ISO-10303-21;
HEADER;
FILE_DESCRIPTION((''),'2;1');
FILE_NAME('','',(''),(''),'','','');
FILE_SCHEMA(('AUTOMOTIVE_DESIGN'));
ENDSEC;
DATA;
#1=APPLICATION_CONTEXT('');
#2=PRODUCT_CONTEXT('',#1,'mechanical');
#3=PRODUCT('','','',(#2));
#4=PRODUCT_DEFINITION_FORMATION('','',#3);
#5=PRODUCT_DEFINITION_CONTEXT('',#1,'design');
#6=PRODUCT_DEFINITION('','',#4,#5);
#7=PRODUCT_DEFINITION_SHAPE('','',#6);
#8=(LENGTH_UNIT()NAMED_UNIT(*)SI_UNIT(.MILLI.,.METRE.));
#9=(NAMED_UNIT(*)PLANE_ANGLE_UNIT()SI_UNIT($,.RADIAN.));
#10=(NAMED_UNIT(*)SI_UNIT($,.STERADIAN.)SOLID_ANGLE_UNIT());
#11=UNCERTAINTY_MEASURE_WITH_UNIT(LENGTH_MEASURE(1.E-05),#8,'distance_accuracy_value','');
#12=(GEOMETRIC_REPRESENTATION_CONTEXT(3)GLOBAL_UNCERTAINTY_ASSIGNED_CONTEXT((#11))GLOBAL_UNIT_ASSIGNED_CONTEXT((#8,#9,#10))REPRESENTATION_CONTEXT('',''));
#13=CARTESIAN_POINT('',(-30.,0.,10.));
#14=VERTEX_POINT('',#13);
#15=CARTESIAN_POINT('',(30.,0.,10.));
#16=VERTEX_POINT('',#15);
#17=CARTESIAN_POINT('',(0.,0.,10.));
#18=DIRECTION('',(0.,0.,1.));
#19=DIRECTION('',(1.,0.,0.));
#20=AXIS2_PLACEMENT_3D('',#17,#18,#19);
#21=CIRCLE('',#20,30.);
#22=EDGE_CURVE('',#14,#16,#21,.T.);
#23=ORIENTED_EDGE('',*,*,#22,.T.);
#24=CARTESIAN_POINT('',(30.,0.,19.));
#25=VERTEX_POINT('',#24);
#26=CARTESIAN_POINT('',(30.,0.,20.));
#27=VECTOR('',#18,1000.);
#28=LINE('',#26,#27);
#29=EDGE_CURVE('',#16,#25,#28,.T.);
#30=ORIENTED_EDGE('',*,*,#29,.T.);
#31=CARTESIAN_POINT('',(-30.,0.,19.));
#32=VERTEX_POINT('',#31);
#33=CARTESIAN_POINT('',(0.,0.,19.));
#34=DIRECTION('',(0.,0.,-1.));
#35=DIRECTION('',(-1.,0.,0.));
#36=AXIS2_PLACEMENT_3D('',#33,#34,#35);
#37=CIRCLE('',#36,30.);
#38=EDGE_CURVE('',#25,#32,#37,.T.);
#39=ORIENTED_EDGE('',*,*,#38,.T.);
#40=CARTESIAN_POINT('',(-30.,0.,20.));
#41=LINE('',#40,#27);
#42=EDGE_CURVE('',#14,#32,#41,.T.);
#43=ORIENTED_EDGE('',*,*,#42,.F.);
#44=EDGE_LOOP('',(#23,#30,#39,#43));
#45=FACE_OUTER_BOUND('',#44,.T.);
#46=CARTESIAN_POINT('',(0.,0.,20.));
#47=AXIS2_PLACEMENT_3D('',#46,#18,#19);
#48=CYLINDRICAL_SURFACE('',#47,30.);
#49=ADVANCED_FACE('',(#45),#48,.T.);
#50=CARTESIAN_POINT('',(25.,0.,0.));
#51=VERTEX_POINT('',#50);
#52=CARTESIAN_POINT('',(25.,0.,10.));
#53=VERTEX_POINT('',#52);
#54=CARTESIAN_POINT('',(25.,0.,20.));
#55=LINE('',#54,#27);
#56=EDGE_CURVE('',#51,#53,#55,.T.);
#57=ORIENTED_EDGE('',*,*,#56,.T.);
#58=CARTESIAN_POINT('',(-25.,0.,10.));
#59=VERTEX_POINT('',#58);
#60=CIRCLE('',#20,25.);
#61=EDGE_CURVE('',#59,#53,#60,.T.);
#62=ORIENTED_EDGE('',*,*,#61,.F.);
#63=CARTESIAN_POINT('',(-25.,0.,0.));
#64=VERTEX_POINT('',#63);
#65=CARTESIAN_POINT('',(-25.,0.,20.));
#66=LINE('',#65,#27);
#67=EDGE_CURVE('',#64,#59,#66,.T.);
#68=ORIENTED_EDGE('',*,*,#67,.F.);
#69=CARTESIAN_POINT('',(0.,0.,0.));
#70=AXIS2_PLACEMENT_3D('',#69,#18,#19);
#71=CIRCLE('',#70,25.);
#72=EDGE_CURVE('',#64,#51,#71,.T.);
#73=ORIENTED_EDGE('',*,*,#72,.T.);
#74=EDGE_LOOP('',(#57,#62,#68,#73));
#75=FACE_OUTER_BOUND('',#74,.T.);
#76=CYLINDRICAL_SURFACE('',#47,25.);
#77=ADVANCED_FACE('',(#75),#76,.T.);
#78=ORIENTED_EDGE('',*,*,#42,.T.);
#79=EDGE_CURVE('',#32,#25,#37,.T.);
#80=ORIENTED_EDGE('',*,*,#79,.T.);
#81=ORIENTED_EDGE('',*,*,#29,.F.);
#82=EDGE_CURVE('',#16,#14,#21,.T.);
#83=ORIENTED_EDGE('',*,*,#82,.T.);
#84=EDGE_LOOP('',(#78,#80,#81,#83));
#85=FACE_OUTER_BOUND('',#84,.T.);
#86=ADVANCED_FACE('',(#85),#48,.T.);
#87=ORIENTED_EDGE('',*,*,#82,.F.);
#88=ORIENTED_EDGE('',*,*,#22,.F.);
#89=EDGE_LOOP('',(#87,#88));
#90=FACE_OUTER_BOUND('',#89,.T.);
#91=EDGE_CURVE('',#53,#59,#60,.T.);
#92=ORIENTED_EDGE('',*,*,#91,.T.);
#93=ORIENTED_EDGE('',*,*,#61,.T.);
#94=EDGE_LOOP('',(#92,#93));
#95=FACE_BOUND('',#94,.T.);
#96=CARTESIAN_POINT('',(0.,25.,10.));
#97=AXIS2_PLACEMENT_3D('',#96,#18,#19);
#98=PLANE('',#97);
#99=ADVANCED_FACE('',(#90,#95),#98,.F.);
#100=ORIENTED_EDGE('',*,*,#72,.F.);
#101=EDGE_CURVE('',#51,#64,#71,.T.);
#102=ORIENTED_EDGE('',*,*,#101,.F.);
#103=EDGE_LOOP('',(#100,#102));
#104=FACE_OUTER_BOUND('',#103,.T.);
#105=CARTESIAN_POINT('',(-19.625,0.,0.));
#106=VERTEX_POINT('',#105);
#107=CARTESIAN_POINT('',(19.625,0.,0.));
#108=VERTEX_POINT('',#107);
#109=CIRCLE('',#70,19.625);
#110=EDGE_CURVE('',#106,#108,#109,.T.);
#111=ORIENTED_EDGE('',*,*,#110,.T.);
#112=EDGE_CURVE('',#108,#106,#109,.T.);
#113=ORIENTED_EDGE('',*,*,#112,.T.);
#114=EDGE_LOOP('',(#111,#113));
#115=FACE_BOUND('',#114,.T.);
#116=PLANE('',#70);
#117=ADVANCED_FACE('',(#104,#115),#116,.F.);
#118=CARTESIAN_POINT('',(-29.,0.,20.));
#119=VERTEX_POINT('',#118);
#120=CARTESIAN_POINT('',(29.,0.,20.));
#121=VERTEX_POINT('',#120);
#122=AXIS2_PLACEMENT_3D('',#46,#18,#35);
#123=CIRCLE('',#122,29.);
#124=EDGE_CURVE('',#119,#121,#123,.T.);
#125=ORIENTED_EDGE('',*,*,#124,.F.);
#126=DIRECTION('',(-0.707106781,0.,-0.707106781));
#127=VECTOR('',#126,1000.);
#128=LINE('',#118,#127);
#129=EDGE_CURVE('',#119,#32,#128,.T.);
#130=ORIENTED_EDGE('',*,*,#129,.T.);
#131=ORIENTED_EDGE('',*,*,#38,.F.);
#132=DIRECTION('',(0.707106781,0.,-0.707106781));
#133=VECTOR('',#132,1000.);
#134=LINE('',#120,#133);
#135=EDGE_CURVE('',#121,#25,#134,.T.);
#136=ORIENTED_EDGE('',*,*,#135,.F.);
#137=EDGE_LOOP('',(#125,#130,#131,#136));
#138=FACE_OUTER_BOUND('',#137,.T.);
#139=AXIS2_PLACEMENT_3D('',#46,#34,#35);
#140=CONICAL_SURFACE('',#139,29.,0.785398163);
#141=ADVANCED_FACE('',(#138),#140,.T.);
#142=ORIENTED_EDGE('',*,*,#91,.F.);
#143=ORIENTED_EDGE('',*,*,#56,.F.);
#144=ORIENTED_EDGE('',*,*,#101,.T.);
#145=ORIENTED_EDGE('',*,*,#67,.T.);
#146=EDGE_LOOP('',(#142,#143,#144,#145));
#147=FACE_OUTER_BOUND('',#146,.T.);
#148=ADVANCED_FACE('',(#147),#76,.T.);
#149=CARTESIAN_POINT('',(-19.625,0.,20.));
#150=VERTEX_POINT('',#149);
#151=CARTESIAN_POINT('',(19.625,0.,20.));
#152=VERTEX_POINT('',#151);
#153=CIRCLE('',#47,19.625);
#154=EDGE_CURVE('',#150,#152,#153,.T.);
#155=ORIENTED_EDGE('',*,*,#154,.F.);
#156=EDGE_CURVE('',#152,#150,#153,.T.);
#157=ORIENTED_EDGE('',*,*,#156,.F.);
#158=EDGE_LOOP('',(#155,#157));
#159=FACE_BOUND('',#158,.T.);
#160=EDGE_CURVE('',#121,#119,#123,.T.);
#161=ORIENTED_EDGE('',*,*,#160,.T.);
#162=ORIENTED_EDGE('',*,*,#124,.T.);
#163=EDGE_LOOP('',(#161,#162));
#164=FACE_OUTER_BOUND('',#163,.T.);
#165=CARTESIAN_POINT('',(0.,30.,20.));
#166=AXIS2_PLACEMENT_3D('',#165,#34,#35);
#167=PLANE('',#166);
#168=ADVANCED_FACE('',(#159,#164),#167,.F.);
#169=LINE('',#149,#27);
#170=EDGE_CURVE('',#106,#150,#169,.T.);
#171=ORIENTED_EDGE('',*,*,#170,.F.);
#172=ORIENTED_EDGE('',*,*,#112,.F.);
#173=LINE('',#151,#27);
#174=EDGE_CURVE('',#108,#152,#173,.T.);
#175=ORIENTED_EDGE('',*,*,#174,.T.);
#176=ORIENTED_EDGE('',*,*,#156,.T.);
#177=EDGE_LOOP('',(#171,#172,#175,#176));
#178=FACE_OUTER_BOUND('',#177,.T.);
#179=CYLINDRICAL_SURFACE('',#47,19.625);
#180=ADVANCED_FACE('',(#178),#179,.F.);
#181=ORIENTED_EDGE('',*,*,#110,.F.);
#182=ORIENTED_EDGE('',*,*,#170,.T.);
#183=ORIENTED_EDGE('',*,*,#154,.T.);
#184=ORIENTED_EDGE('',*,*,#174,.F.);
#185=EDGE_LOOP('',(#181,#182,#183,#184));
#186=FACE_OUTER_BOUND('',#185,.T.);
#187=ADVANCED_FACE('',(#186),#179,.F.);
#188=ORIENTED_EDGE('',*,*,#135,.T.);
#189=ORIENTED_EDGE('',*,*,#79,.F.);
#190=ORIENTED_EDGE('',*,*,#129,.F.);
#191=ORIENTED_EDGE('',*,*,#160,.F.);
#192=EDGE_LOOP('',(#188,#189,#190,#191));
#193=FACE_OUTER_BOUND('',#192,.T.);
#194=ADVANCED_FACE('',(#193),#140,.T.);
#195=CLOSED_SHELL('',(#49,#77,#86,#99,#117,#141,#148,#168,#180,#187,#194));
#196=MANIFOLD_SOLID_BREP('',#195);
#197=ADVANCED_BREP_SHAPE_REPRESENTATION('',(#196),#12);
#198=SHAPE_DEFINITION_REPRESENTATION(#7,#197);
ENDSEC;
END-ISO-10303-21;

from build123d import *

# Parameters (mm, degrees)
G1_1_4_TAPPED_HOLE1_D = 39.25
CHAMFER1_SIZE         = 1


with BuildPart() as part:
    # Sketch1 → Revolve1 (revolve)
    with BuildSketch(Plane(origin=(0, 0, 0), x_dir=(0, 0, -1), z_dir=(1, 0, 0)), mode=Mode.PRIVATE) as revolve1_sk:
        Polygon((0, 0), (0, 25), (-10, 25), (-10, 30), (-20, 30), (-20, 0), align=None)
    revolve(revolve1_sk.sketch.rotate(Axis((0, 0, 20), (0, 0, -1)), 90), axis=Axis((0, 0, 20), (0, 0, -1)))

    # G1-1/4 Tapped Hole1 (through all)
    with Locations(Plane.XY.offset(20)):
        with Locations((0, 0)):
            Hole(G1_1_4_TAPPED_HOLE1_D / 2)

    # Chamfer1
    chamfer1_edges = [part.edges().sort_by_distance(p)[0] for p in [
        (-30, 0, 20),
    ]]
    chamfer(chamfer1_edges, length=CHAMFER1_SIZE)


solid = part.part
